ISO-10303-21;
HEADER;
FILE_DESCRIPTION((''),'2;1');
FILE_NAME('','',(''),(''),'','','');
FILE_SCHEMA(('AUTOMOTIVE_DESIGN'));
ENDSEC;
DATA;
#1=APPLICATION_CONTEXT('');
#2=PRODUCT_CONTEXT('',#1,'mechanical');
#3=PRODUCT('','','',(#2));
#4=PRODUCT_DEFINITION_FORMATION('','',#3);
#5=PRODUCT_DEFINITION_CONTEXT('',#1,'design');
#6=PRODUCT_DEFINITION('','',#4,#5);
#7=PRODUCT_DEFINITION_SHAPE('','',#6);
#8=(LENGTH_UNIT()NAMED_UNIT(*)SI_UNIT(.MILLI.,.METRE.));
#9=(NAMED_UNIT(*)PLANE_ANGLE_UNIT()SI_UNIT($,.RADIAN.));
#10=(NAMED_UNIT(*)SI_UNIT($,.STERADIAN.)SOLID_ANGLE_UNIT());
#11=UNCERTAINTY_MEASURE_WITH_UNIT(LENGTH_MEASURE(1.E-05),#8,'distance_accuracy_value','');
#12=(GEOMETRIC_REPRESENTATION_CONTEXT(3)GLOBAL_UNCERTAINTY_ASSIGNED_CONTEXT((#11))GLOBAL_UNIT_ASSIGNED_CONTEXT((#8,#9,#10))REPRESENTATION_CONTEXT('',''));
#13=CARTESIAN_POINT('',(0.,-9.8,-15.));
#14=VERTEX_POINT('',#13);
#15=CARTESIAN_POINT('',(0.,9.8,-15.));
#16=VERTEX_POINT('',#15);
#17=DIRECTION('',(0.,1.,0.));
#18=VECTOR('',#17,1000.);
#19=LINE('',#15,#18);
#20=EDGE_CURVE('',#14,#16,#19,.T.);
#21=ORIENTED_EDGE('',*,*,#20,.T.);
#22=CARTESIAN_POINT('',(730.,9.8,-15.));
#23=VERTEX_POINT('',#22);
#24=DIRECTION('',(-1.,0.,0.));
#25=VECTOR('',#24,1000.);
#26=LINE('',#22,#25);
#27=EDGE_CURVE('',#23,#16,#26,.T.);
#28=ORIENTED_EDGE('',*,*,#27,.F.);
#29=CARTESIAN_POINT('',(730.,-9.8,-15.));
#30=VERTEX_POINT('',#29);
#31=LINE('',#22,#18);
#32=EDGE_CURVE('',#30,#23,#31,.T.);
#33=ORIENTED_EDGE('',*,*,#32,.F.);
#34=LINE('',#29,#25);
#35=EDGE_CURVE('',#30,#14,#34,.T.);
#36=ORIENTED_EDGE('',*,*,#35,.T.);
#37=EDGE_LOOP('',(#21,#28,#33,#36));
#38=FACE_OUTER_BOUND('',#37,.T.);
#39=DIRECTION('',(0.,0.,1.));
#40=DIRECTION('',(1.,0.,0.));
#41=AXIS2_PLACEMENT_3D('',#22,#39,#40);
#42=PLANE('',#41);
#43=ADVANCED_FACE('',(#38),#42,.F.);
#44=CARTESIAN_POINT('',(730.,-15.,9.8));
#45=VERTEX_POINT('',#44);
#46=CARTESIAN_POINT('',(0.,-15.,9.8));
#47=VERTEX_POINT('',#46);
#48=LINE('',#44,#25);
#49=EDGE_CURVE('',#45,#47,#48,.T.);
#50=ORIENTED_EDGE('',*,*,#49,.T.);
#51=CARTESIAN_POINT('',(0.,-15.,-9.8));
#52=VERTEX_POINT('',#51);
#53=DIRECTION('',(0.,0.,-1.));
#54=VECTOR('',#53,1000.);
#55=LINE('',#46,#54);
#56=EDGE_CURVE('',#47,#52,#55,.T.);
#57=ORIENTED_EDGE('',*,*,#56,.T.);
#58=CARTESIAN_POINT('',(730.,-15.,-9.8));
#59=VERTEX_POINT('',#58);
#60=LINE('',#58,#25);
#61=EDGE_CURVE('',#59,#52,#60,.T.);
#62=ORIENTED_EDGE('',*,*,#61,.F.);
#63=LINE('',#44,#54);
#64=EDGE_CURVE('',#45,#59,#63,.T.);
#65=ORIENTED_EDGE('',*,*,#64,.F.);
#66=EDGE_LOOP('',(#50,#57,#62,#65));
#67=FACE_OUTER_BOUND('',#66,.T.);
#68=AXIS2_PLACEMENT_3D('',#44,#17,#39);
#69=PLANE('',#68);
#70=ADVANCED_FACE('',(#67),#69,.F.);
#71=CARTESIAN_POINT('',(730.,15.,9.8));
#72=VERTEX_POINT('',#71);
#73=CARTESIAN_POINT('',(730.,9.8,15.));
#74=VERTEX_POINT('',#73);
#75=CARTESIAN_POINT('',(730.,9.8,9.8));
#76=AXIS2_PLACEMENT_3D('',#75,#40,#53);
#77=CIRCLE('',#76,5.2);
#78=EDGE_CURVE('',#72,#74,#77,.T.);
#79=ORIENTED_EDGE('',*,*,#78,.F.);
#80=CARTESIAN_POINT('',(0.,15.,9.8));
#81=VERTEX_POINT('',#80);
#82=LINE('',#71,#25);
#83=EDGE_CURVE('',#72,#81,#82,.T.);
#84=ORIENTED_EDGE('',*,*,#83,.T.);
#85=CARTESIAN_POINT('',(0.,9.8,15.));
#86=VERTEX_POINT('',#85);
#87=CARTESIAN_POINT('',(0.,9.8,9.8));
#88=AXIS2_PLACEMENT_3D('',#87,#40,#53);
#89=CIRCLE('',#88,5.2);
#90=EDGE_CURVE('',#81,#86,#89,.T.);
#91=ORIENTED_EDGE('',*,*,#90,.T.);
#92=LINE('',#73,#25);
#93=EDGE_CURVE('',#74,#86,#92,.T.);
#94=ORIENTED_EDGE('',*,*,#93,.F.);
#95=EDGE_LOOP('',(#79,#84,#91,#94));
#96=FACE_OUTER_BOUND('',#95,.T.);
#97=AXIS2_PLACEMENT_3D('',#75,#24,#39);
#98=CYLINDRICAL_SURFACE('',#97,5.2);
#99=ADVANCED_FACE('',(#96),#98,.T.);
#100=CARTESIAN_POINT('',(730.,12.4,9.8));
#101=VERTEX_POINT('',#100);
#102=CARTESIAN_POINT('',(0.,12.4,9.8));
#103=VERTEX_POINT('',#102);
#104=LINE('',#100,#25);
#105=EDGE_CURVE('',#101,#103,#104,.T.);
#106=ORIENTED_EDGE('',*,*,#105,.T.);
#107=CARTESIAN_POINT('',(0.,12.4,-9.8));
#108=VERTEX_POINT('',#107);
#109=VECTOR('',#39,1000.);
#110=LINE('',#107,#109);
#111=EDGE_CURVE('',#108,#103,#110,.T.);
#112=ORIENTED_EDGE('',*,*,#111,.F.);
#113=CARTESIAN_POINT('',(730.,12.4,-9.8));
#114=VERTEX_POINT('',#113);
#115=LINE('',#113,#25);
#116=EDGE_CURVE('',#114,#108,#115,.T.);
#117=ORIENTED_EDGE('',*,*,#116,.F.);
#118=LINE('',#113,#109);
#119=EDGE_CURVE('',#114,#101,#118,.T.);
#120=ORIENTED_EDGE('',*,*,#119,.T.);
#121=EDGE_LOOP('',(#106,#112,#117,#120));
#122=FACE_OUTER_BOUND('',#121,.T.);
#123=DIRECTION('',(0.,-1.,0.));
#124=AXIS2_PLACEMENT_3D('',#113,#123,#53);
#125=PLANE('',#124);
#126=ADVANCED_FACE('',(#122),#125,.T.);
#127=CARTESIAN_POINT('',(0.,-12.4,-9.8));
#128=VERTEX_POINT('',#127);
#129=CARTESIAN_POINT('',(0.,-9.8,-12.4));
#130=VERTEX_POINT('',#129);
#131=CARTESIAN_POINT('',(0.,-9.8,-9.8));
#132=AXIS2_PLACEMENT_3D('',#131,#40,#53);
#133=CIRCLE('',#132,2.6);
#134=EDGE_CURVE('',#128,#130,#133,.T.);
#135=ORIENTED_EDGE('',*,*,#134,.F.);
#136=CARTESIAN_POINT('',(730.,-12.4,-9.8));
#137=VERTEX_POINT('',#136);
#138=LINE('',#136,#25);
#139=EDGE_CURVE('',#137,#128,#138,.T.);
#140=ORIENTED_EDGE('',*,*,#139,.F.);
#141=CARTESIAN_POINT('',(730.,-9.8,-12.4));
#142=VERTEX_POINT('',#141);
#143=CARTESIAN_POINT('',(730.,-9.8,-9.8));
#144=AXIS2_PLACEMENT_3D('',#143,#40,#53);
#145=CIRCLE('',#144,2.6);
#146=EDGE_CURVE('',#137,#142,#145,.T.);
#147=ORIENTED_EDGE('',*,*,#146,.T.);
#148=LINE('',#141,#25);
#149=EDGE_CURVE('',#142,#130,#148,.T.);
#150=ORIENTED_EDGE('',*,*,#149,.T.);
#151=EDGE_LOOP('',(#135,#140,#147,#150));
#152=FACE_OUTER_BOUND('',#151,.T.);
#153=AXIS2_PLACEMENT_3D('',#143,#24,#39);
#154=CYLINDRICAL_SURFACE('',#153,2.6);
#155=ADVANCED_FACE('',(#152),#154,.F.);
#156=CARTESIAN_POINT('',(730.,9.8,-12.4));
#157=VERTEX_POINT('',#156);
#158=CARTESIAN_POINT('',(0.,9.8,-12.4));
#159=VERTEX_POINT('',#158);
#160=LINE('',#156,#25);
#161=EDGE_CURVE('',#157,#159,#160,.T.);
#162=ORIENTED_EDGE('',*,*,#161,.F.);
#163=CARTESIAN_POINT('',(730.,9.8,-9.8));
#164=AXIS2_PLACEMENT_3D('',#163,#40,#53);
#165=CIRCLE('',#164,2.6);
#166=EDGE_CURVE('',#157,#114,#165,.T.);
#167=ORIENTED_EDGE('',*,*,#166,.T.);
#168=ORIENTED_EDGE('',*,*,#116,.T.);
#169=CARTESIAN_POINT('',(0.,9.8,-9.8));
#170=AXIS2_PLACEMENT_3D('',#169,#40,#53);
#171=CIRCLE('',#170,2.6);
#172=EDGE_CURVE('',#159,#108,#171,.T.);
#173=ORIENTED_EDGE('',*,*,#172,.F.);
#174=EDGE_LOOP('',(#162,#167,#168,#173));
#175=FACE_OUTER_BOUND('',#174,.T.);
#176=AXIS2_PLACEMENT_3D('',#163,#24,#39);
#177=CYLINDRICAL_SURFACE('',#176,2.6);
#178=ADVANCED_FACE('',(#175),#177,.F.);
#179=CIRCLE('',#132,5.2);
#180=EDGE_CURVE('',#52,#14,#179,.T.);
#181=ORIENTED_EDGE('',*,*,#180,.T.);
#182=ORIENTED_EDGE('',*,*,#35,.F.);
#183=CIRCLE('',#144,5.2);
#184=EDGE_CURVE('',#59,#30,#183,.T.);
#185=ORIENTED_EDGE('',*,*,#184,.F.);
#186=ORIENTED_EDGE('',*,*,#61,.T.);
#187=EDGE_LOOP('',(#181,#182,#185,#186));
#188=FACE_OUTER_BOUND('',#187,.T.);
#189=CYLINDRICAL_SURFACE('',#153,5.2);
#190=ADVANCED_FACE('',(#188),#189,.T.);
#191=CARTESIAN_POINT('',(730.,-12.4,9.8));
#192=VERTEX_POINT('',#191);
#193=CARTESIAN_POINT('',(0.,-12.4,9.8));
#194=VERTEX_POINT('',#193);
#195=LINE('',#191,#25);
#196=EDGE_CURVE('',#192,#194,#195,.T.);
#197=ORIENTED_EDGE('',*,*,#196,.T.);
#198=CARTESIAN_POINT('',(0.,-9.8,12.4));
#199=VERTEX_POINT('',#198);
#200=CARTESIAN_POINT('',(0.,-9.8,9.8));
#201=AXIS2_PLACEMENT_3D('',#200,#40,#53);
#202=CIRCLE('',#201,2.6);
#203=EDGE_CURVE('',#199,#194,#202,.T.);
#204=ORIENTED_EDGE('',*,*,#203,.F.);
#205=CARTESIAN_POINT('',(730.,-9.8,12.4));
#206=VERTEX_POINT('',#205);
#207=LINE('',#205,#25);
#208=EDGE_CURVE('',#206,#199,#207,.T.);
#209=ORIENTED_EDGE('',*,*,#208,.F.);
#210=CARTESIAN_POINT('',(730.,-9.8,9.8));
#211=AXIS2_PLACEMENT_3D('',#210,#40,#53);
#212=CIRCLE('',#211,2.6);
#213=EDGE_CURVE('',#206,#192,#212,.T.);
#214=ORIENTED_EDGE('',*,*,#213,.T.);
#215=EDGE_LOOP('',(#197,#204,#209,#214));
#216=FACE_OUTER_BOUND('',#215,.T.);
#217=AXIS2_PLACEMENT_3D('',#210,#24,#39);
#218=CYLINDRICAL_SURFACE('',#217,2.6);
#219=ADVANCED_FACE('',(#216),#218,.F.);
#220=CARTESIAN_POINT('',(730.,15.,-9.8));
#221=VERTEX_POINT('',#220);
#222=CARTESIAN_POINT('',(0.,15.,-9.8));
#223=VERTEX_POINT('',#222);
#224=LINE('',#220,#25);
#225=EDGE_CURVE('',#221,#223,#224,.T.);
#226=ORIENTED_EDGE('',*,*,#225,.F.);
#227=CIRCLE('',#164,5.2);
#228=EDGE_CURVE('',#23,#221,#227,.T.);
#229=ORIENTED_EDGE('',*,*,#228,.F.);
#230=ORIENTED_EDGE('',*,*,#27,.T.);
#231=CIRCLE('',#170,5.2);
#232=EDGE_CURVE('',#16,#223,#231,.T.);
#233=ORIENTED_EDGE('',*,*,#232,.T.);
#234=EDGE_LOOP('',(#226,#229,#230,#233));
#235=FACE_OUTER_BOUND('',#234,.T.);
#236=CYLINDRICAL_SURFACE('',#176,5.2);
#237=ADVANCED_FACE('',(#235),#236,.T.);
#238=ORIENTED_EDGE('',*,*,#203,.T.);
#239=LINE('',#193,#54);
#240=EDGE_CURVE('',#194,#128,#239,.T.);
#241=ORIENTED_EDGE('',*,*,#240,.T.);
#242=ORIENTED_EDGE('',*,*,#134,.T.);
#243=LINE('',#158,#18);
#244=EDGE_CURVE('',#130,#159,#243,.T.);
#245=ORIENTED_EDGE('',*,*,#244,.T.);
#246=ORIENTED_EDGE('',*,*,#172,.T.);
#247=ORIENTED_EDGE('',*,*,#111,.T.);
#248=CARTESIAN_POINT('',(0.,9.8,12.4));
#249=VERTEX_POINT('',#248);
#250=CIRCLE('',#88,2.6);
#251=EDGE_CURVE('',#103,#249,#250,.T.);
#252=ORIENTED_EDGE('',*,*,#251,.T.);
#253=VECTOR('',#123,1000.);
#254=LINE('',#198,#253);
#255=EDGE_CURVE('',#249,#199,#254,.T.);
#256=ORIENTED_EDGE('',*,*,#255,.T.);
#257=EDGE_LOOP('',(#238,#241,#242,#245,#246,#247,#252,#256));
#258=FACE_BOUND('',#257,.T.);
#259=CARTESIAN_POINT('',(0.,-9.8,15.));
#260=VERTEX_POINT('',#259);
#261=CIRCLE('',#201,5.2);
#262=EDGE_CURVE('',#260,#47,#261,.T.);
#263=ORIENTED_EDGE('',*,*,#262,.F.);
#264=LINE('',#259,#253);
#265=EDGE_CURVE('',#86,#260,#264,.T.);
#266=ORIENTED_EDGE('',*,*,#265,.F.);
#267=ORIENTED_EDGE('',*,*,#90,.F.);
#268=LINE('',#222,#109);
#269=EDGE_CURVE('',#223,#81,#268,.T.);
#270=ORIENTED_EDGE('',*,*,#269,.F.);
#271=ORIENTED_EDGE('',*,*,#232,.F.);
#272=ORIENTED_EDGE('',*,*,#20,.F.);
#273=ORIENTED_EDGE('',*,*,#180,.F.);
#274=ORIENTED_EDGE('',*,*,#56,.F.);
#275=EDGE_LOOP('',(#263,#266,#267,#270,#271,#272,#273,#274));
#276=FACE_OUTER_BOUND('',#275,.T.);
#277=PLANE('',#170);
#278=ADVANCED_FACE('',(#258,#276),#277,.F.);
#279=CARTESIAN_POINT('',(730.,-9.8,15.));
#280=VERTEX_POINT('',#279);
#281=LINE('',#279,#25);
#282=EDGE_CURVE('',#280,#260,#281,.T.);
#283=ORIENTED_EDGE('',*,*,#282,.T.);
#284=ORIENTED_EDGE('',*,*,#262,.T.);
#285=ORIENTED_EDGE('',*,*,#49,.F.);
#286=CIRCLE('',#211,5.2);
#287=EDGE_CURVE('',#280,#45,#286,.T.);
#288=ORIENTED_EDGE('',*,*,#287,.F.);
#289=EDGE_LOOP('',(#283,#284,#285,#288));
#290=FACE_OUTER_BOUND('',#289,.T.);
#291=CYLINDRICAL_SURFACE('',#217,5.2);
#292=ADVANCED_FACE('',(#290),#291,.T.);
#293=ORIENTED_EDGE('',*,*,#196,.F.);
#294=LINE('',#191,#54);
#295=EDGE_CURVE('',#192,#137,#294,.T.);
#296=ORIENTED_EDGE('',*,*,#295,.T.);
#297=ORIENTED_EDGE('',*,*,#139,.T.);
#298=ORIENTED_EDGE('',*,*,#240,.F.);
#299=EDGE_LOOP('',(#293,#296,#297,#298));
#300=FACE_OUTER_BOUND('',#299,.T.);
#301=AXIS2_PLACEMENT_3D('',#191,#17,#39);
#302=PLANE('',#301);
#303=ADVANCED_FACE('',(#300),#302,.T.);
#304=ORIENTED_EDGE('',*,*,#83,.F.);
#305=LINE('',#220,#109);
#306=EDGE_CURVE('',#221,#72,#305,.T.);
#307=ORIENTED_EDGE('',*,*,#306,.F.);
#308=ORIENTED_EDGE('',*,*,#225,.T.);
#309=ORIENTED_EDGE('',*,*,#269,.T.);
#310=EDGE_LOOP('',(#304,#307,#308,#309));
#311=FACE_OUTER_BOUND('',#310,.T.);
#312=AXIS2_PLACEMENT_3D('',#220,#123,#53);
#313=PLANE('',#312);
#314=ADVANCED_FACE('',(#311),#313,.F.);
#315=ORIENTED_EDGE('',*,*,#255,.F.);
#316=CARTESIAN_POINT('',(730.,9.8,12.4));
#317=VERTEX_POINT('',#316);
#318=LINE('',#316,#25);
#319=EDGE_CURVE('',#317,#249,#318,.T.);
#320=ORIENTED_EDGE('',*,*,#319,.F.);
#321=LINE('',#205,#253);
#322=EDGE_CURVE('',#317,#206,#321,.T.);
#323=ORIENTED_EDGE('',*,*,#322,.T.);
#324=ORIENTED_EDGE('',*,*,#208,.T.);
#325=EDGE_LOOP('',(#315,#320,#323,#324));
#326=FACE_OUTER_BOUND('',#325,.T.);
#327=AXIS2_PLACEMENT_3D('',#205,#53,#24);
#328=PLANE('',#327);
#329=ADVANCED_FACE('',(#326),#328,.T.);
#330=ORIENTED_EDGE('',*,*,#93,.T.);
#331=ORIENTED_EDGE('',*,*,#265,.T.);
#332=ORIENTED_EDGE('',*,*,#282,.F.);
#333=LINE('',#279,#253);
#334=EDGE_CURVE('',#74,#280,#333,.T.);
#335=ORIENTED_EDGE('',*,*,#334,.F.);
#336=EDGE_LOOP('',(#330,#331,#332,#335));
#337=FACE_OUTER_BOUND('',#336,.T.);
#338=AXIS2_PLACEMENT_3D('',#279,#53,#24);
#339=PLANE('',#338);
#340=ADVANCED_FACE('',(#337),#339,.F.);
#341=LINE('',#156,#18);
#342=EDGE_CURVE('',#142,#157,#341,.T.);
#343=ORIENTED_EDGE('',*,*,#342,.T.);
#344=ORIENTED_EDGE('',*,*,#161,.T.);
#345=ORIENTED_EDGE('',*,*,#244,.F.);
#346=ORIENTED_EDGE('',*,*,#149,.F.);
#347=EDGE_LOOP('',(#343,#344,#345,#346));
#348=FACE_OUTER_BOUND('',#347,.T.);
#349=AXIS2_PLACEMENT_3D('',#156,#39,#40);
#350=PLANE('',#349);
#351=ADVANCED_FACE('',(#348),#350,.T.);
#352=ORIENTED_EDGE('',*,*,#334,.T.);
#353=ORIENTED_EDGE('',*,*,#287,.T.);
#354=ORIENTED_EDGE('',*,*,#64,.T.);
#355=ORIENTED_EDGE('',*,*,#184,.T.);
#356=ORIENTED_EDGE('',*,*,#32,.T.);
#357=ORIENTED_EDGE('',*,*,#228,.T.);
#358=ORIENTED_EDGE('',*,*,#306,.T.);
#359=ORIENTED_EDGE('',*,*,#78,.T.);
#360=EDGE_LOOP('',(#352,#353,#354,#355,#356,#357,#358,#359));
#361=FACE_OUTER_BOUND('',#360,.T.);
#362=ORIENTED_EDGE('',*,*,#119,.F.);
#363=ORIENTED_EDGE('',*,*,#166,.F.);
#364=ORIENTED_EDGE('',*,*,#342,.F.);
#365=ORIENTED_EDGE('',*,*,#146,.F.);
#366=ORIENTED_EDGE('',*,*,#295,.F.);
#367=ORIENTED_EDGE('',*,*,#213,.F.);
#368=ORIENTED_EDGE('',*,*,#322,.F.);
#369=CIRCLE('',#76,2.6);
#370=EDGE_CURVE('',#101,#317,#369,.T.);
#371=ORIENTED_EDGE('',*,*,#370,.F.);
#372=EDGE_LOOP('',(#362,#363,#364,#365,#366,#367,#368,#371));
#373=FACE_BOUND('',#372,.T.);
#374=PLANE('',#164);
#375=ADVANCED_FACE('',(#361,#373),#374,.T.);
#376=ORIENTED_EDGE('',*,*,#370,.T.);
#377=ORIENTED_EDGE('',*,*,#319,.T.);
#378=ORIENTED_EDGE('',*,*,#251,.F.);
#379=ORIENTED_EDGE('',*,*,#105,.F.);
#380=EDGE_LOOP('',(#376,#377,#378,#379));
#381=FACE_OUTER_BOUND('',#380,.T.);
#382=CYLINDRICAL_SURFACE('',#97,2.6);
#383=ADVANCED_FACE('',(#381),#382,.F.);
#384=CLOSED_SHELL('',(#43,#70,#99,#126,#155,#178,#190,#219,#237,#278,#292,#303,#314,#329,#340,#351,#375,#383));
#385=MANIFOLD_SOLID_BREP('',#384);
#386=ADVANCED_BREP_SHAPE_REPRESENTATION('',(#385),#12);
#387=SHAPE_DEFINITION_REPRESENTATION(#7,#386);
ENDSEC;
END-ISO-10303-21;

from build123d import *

# Parameters (mm, degrees)
MEMBER_1_DEPTH = 730


with BuildPart() as part:
    # Sketch1 → Member 1 (new body)
    with BuildSketch(Plane(origin=(0, 0, 0), x_dir=(0, 0, -1), z_dir=(1, 0, 0))):
        with BuildLine():
            Line((-9.8, -15), (9.8, -15))
            ThreePointArc((9.8, -15), (13.476955262, -13.476955262), (15, -9.8))
            Line((15, -9.8), (15, 9.8))
            ThreePointArc((15, 9.8), (13.476955262, 13.476955262), (9.8, 15))
            Line((9.8, 15), (-9.8, 15))
            ThreePointArc((-9.8, 15), (-13.476955262, 13.476955262), (-15, 9.8))
            Line((-15, 9.8), (-15, -9.8))
            ThreePointArc((-15, -9.8), (-13.476955262, -13.476955262), (-9.8, -15))
        make_face()
        with BuildLine():
            Line((-9.8, -12.4), (9.8, -12.4))
            ThreePointArc((9.8, -12.4), (11.638477631, -11.638477631), (12.4, -9.8))
            Line((12.4, -9.8), (12.4, 9.8))
            ThreePointArc((12.4, 9.8), (11.638477631, 11.638477631), (9.8, 12.4))
            Line((9.8, 12.4), (-9.8, 12.4))
            ThreePointArc((-9.8, 12.4), (-11.638477631, 11.638477631), (-12.4, 9.8))
            Line((-12.4, 9.8), (-12.4, -9.8))
            ThreePointArc((-12.4, -9.8), (-11.638477631, -11.638477631), (-9.8, -12.4))
        make_face(mode=Mode.SUBTRACT)
    extrude(amount=MEMBER_1_DEPTH)


solid = part.part
